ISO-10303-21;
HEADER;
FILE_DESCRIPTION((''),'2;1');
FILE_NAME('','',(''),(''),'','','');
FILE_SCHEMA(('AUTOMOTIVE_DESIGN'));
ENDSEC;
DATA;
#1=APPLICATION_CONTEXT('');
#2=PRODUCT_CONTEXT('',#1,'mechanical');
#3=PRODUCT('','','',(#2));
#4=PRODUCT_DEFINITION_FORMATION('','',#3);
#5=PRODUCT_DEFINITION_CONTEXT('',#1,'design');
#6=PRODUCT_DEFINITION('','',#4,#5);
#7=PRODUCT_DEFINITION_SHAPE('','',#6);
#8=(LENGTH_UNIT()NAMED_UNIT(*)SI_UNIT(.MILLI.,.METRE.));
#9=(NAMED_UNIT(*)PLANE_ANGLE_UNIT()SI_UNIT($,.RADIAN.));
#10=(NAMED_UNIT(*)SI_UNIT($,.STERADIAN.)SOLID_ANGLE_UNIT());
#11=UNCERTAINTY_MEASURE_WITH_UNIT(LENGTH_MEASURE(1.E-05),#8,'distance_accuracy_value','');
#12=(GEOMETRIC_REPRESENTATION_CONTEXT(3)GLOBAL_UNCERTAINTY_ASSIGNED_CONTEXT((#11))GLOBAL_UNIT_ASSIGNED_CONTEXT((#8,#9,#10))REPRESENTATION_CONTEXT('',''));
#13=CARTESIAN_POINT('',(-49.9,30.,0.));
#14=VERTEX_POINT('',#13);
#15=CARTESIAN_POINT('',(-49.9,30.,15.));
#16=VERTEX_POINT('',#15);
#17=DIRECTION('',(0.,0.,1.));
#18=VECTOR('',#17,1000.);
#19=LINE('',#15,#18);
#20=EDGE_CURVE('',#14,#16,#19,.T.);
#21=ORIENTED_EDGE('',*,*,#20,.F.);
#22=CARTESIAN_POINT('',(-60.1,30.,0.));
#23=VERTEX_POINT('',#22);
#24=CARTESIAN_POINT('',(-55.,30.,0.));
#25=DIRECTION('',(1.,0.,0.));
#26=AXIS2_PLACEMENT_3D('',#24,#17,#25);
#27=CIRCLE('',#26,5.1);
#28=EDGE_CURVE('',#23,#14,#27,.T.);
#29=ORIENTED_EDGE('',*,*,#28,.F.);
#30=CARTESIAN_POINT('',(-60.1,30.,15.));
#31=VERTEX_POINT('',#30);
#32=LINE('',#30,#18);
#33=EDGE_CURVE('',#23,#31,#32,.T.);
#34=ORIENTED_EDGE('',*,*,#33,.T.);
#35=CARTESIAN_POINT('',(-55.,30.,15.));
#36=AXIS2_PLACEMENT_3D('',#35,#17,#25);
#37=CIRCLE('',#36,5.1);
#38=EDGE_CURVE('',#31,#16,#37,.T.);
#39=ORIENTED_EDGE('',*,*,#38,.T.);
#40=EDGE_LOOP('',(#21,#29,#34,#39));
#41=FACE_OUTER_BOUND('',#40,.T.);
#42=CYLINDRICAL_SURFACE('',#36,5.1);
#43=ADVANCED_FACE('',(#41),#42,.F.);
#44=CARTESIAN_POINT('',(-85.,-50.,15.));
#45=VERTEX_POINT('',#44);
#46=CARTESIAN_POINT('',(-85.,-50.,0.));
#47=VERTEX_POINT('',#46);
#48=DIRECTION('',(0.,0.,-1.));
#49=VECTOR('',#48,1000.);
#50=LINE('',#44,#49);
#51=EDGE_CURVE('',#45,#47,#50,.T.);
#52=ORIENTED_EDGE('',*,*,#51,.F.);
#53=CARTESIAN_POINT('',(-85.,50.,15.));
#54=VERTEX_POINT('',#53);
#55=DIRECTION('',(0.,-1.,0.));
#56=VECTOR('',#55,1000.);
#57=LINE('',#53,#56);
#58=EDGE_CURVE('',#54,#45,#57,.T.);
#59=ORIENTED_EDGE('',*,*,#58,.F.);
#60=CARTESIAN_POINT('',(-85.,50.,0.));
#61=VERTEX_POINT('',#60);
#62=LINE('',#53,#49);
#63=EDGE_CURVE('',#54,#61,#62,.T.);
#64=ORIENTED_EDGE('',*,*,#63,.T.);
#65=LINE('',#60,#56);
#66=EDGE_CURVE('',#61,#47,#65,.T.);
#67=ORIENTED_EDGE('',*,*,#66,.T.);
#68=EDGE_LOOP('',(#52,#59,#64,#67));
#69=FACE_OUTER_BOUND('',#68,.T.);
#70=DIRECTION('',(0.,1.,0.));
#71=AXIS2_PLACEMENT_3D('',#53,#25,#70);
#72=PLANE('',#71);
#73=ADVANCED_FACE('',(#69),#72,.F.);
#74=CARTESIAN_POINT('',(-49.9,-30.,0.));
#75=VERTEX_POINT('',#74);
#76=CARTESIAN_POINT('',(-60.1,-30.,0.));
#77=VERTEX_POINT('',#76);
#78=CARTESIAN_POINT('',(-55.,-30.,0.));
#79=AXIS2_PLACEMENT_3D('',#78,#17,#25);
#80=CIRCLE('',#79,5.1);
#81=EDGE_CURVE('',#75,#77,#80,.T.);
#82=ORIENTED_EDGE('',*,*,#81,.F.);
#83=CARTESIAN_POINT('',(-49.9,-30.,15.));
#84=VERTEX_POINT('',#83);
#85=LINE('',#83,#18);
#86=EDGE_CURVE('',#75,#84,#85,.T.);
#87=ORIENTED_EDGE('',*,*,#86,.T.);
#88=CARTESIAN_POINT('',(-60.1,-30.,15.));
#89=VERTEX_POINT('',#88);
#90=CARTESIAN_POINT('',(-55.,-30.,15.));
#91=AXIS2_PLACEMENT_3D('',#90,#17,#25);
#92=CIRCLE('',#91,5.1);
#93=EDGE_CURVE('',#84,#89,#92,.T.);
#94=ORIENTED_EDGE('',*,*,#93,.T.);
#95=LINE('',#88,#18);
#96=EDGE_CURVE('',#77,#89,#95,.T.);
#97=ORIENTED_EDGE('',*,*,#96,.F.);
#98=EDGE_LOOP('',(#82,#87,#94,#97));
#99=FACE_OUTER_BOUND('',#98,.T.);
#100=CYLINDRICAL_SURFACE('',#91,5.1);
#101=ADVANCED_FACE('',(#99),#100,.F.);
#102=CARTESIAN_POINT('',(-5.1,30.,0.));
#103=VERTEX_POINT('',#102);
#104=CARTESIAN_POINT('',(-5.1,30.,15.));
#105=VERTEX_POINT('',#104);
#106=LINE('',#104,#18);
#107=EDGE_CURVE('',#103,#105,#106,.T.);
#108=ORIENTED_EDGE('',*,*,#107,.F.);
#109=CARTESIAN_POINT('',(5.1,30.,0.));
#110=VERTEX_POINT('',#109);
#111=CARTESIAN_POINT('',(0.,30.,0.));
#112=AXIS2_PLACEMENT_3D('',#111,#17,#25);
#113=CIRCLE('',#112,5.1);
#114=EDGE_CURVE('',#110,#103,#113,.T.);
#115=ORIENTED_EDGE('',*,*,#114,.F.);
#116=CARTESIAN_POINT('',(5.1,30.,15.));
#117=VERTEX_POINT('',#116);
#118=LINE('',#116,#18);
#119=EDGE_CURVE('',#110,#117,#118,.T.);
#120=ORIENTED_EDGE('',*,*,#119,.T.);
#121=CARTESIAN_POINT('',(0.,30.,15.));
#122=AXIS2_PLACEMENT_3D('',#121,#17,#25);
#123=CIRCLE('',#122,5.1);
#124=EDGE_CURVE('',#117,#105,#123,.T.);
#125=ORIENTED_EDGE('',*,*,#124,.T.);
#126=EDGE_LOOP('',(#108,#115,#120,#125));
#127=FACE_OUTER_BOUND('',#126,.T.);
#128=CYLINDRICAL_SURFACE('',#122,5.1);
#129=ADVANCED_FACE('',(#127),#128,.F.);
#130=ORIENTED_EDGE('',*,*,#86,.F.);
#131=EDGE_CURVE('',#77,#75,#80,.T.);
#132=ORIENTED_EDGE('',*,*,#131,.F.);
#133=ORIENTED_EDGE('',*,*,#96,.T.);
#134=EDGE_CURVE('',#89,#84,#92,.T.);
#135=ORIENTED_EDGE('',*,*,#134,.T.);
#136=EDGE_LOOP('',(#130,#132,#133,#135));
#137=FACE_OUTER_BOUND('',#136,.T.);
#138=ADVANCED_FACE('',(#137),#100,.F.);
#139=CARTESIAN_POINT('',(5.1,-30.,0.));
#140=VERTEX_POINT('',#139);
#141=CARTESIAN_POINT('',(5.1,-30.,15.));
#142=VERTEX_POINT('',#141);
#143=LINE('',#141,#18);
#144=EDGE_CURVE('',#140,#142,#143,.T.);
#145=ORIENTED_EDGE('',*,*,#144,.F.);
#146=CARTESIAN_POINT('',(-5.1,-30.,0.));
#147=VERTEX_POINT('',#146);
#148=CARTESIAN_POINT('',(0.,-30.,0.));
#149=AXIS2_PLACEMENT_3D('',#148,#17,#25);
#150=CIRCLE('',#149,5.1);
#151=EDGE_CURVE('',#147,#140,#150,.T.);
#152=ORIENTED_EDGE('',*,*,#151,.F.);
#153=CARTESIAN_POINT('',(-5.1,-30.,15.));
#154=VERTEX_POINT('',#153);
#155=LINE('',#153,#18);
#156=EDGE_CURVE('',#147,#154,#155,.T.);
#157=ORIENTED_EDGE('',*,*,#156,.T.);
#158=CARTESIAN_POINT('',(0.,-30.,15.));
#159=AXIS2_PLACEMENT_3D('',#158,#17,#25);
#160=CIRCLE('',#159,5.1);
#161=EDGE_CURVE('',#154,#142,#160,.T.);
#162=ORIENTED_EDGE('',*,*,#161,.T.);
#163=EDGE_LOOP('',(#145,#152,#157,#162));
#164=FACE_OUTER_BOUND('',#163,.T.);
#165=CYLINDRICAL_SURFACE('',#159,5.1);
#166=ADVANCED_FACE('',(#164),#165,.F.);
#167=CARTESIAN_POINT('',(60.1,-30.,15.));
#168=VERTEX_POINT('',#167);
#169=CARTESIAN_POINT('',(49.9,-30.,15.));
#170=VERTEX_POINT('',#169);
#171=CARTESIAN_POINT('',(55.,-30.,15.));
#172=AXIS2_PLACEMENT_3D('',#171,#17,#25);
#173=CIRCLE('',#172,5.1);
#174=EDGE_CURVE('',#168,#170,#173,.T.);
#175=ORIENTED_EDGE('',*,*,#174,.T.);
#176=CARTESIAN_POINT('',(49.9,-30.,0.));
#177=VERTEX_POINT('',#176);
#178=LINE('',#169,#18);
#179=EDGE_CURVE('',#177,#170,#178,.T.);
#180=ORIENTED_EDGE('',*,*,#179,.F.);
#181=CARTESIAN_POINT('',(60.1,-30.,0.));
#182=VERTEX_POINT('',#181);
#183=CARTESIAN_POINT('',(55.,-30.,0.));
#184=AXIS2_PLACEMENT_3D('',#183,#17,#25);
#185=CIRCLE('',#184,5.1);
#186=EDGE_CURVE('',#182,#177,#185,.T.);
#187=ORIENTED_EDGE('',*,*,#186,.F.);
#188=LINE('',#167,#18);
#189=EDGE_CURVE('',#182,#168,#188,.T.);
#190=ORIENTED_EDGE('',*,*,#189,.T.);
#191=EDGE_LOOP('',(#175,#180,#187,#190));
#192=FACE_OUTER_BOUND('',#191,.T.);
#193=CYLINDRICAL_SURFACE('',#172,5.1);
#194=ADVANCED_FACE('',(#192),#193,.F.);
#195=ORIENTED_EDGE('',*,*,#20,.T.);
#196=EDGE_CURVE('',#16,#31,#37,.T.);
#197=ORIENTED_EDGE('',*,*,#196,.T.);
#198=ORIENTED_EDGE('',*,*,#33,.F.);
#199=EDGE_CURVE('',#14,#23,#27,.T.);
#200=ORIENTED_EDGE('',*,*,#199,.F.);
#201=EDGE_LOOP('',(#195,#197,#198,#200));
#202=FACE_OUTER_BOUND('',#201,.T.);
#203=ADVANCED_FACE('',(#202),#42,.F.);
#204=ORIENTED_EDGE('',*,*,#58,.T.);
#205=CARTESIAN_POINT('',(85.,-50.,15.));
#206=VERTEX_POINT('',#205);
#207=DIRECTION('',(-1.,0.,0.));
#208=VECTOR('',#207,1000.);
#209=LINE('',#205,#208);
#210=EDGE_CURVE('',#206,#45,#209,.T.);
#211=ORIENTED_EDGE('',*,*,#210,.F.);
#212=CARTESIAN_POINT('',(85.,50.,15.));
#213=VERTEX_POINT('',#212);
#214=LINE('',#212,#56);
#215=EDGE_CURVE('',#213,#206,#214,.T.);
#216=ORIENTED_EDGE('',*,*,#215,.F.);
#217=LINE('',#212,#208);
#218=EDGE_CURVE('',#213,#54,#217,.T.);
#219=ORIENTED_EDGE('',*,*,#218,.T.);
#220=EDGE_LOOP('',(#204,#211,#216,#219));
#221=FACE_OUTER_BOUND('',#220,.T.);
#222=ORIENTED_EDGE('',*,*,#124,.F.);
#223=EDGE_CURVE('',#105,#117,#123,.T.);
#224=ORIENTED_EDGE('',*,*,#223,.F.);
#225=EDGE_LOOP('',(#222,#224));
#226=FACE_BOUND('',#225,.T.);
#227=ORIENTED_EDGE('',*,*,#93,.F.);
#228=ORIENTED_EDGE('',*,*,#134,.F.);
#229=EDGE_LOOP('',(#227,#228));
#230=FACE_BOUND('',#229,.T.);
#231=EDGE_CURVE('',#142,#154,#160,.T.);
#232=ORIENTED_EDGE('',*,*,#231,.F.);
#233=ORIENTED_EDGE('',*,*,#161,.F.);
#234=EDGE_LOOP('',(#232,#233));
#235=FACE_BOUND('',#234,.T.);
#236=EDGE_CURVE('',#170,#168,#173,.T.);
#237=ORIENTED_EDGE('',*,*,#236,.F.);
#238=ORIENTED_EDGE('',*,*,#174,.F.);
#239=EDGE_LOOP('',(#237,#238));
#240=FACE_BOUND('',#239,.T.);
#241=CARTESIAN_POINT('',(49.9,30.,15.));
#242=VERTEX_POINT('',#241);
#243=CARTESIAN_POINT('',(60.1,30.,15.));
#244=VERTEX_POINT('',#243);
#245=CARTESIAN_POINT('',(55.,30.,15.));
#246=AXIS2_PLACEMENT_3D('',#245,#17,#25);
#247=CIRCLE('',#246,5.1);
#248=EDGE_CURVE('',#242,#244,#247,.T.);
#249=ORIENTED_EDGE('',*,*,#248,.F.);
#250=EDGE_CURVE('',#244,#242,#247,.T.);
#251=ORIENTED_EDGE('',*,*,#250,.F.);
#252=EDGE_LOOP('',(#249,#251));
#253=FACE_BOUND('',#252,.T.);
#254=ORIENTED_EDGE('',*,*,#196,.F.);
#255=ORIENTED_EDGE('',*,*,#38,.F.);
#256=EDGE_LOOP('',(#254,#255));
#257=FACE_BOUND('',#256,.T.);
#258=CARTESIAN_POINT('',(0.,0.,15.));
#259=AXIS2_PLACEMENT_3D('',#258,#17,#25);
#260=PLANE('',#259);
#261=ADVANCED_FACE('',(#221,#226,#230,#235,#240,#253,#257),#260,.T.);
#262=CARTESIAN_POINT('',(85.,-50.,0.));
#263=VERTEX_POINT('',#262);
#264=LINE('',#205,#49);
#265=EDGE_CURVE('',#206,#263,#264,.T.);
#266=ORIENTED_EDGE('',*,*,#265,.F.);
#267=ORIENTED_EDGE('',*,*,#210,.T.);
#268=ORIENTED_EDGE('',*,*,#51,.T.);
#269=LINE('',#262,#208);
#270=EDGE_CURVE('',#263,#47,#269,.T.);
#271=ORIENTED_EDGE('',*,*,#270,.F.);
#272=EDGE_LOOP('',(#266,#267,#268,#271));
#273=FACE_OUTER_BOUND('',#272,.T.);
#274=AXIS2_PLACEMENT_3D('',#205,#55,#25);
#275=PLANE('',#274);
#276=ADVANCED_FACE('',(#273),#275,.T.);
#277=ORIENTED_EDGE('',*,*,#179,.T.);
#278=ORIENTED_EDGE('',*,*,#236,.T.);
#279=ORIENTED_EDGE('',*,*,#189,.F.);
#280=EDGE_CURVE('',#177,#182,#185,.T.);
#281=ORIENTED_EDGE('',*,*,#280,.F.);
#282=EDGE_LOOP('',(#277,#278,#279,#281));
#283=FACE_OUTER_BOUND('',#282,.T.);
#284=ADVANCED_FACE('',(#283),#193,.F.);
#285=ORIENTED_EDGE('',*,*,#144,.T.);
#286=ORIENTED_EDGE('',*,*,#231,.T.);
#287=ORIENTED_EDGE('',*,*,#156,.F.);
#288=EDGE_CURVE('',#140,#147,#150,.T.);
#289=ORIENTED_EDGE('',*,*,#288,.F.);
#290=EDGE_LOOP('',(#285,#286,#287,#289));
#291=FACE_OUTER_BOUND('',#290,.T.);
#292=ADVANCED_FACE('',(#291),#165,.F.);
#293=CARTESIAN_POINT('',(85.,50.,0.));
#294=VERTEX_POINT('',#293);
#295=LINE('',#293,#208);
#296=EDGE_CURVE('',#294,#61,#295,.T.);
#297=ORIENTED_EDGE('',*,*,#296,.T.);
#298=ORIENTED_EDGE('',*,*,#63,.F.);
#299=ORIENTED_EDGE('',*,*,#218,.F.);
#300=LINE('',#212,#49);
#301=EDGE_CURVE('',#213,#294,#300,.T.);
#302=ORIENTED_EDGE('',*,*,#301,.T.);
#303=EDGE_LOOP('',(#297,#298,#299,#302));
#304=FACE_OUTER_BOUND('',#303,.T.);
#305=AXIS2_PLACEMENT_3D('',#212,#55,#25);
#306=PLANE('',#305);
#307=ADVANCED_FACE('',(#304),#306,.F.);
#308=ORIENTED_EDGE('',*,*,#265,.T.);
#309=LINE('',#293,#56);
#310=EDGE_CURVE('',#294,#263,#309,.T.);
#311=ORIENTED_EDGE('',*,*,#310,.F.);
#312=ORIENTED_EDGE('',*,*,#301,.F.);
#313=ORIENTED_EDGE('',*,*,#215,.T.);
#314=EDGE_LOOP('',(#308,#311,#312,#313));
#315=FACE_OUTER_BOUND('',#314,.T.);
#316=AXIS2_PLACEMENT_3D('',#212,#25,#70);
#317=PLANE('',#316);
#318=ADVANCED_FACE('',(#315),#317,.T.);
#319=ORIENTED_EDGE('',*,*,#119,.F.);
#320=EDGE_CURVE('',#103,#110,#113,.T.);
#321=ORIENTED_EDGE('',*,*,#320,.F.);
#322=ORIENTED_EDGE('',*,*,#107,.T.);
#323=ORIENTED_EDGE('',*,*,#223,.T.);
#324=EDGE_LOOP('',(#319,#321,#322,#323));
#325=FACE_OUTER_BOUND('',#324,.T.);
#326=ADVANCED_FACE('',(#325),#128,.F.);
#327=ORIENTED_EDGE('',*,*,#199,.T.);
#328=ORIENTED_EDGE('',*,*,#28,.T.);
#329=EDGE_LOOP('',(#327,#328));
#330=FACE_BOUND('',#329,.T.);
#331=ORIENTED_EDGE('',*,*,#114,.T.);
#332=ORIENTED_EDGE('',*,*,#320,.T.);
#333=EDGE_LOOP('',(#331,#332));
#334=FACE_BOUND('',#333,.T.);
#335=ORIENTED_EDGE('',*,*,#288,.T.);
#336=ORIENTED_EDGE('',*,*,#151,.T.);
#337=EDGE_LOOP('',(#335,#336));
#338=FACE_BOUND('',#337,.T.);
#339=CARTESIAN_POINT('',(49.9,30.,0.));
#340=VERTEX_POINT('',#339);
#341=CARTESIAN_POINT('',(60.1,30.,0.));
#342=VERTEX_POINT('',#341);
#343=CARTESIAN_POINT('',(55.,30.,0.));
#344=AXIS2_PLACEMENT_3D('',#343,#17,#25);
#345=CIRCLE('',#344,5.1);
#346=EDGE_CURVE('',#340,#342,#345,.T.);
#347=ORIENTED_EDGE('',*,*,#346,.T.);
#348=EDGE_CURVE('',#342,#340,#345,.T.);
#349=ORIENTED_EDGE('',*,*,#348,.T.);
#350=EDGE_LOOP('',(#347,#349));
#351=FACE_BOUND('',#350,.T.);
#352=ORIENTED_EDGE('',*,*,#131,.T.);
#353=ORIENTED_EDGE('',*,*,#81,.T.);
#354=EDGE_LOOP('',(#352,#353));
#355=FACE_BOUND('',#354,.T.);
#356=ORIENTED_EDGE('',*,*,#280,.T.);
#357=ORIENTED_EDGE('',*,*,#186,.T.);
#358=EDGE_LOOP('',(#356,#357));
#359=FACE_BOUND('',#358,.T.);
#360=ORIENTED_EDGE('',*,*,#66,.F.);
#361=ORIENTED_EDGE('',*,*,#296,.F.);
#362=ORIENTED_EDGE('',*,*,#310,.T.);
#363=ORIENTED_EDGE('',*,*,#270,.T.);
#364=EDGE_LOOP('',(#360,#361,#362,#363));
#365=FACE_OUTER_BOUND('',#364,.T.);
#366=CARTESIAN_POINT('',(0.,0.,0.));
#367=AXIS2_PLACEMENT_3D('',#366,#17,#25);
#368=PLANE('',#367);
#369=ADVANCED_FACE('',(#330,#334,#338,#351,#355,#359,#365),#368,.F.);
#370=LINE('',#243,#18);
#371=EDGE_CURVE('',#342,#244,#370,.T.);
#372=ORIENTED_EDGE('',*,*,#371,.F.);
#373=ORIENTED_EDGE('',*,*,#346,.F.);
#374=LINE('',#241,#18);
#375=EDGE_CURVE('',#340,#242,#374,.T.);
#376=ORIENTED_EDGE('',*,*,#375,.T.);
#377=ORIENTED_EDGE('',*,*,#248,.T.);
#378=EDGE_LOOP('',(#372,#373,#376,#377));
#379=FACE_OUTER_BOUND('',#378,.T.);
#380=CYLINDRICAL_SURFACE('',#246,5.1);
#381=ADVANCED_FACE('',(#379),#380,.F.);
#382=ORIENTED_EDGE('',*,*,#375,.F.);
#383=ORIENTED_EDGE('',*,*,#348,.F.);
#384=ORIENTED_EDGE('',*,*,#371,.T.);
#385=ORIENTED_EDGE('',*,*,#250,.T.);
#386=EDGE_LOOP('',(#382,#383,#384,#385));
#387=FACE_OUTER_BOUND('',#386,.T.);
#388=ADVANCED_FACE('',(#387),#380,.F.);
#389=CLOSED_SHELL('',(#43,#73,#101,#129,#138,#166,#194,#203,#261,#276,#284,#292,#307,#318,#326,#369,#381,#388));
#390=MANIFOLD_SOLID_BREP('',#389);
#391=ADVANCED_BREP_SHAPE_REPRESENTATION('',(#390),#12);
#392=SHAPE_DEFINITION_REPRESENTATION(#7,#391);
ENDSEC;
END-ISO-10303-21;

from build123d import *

# Parameters (mm, degrees)
SKETCH1_W              = 170
SKETCH1_H              = 100
BOSS_EXTRUDE1_DEPTH    = 15
M12_TAPPED_HOLE1_D     = 10.2
M12_TAPPED_HOLE1_DEPTH = 29.25
M12_TAPPED_HOLE1_TIP   = 3.064389157


with BuildPart() as part:
    # Sketch1 → Boss-Extrude1 (new body)
    with BuildSketch(Plane.XY):
        Rectangle(SKETCH1_W, SKETCH1_H)
    extrude(amount=BOSS_EXTRUDE1_DEPTH)

    # M12 Tapped Hole1
    with Locations(Plane.XY.offset(15)):
        with Locations((-55, 30), (0, 30), (55, 30), (55, -30), (0, -30), (-55, -30)):
            Hole(M12_TAPPED_HOLE1_D / 2, depth=M12_TAPPED_HOLE1_DEPTH)
            with Locations((0, 0, -(M12_TAPPED_HOLE1_DEPTH + M12_TAPPED_HOLE1_TIP / 2))):  # 118° drill point
                Cone(0, M12_TAPPED_HOLE1_D / 2, M12_TAPPED_HOLE1_TIP, mode=Mode.SUBTRACT)


solid = part.part
